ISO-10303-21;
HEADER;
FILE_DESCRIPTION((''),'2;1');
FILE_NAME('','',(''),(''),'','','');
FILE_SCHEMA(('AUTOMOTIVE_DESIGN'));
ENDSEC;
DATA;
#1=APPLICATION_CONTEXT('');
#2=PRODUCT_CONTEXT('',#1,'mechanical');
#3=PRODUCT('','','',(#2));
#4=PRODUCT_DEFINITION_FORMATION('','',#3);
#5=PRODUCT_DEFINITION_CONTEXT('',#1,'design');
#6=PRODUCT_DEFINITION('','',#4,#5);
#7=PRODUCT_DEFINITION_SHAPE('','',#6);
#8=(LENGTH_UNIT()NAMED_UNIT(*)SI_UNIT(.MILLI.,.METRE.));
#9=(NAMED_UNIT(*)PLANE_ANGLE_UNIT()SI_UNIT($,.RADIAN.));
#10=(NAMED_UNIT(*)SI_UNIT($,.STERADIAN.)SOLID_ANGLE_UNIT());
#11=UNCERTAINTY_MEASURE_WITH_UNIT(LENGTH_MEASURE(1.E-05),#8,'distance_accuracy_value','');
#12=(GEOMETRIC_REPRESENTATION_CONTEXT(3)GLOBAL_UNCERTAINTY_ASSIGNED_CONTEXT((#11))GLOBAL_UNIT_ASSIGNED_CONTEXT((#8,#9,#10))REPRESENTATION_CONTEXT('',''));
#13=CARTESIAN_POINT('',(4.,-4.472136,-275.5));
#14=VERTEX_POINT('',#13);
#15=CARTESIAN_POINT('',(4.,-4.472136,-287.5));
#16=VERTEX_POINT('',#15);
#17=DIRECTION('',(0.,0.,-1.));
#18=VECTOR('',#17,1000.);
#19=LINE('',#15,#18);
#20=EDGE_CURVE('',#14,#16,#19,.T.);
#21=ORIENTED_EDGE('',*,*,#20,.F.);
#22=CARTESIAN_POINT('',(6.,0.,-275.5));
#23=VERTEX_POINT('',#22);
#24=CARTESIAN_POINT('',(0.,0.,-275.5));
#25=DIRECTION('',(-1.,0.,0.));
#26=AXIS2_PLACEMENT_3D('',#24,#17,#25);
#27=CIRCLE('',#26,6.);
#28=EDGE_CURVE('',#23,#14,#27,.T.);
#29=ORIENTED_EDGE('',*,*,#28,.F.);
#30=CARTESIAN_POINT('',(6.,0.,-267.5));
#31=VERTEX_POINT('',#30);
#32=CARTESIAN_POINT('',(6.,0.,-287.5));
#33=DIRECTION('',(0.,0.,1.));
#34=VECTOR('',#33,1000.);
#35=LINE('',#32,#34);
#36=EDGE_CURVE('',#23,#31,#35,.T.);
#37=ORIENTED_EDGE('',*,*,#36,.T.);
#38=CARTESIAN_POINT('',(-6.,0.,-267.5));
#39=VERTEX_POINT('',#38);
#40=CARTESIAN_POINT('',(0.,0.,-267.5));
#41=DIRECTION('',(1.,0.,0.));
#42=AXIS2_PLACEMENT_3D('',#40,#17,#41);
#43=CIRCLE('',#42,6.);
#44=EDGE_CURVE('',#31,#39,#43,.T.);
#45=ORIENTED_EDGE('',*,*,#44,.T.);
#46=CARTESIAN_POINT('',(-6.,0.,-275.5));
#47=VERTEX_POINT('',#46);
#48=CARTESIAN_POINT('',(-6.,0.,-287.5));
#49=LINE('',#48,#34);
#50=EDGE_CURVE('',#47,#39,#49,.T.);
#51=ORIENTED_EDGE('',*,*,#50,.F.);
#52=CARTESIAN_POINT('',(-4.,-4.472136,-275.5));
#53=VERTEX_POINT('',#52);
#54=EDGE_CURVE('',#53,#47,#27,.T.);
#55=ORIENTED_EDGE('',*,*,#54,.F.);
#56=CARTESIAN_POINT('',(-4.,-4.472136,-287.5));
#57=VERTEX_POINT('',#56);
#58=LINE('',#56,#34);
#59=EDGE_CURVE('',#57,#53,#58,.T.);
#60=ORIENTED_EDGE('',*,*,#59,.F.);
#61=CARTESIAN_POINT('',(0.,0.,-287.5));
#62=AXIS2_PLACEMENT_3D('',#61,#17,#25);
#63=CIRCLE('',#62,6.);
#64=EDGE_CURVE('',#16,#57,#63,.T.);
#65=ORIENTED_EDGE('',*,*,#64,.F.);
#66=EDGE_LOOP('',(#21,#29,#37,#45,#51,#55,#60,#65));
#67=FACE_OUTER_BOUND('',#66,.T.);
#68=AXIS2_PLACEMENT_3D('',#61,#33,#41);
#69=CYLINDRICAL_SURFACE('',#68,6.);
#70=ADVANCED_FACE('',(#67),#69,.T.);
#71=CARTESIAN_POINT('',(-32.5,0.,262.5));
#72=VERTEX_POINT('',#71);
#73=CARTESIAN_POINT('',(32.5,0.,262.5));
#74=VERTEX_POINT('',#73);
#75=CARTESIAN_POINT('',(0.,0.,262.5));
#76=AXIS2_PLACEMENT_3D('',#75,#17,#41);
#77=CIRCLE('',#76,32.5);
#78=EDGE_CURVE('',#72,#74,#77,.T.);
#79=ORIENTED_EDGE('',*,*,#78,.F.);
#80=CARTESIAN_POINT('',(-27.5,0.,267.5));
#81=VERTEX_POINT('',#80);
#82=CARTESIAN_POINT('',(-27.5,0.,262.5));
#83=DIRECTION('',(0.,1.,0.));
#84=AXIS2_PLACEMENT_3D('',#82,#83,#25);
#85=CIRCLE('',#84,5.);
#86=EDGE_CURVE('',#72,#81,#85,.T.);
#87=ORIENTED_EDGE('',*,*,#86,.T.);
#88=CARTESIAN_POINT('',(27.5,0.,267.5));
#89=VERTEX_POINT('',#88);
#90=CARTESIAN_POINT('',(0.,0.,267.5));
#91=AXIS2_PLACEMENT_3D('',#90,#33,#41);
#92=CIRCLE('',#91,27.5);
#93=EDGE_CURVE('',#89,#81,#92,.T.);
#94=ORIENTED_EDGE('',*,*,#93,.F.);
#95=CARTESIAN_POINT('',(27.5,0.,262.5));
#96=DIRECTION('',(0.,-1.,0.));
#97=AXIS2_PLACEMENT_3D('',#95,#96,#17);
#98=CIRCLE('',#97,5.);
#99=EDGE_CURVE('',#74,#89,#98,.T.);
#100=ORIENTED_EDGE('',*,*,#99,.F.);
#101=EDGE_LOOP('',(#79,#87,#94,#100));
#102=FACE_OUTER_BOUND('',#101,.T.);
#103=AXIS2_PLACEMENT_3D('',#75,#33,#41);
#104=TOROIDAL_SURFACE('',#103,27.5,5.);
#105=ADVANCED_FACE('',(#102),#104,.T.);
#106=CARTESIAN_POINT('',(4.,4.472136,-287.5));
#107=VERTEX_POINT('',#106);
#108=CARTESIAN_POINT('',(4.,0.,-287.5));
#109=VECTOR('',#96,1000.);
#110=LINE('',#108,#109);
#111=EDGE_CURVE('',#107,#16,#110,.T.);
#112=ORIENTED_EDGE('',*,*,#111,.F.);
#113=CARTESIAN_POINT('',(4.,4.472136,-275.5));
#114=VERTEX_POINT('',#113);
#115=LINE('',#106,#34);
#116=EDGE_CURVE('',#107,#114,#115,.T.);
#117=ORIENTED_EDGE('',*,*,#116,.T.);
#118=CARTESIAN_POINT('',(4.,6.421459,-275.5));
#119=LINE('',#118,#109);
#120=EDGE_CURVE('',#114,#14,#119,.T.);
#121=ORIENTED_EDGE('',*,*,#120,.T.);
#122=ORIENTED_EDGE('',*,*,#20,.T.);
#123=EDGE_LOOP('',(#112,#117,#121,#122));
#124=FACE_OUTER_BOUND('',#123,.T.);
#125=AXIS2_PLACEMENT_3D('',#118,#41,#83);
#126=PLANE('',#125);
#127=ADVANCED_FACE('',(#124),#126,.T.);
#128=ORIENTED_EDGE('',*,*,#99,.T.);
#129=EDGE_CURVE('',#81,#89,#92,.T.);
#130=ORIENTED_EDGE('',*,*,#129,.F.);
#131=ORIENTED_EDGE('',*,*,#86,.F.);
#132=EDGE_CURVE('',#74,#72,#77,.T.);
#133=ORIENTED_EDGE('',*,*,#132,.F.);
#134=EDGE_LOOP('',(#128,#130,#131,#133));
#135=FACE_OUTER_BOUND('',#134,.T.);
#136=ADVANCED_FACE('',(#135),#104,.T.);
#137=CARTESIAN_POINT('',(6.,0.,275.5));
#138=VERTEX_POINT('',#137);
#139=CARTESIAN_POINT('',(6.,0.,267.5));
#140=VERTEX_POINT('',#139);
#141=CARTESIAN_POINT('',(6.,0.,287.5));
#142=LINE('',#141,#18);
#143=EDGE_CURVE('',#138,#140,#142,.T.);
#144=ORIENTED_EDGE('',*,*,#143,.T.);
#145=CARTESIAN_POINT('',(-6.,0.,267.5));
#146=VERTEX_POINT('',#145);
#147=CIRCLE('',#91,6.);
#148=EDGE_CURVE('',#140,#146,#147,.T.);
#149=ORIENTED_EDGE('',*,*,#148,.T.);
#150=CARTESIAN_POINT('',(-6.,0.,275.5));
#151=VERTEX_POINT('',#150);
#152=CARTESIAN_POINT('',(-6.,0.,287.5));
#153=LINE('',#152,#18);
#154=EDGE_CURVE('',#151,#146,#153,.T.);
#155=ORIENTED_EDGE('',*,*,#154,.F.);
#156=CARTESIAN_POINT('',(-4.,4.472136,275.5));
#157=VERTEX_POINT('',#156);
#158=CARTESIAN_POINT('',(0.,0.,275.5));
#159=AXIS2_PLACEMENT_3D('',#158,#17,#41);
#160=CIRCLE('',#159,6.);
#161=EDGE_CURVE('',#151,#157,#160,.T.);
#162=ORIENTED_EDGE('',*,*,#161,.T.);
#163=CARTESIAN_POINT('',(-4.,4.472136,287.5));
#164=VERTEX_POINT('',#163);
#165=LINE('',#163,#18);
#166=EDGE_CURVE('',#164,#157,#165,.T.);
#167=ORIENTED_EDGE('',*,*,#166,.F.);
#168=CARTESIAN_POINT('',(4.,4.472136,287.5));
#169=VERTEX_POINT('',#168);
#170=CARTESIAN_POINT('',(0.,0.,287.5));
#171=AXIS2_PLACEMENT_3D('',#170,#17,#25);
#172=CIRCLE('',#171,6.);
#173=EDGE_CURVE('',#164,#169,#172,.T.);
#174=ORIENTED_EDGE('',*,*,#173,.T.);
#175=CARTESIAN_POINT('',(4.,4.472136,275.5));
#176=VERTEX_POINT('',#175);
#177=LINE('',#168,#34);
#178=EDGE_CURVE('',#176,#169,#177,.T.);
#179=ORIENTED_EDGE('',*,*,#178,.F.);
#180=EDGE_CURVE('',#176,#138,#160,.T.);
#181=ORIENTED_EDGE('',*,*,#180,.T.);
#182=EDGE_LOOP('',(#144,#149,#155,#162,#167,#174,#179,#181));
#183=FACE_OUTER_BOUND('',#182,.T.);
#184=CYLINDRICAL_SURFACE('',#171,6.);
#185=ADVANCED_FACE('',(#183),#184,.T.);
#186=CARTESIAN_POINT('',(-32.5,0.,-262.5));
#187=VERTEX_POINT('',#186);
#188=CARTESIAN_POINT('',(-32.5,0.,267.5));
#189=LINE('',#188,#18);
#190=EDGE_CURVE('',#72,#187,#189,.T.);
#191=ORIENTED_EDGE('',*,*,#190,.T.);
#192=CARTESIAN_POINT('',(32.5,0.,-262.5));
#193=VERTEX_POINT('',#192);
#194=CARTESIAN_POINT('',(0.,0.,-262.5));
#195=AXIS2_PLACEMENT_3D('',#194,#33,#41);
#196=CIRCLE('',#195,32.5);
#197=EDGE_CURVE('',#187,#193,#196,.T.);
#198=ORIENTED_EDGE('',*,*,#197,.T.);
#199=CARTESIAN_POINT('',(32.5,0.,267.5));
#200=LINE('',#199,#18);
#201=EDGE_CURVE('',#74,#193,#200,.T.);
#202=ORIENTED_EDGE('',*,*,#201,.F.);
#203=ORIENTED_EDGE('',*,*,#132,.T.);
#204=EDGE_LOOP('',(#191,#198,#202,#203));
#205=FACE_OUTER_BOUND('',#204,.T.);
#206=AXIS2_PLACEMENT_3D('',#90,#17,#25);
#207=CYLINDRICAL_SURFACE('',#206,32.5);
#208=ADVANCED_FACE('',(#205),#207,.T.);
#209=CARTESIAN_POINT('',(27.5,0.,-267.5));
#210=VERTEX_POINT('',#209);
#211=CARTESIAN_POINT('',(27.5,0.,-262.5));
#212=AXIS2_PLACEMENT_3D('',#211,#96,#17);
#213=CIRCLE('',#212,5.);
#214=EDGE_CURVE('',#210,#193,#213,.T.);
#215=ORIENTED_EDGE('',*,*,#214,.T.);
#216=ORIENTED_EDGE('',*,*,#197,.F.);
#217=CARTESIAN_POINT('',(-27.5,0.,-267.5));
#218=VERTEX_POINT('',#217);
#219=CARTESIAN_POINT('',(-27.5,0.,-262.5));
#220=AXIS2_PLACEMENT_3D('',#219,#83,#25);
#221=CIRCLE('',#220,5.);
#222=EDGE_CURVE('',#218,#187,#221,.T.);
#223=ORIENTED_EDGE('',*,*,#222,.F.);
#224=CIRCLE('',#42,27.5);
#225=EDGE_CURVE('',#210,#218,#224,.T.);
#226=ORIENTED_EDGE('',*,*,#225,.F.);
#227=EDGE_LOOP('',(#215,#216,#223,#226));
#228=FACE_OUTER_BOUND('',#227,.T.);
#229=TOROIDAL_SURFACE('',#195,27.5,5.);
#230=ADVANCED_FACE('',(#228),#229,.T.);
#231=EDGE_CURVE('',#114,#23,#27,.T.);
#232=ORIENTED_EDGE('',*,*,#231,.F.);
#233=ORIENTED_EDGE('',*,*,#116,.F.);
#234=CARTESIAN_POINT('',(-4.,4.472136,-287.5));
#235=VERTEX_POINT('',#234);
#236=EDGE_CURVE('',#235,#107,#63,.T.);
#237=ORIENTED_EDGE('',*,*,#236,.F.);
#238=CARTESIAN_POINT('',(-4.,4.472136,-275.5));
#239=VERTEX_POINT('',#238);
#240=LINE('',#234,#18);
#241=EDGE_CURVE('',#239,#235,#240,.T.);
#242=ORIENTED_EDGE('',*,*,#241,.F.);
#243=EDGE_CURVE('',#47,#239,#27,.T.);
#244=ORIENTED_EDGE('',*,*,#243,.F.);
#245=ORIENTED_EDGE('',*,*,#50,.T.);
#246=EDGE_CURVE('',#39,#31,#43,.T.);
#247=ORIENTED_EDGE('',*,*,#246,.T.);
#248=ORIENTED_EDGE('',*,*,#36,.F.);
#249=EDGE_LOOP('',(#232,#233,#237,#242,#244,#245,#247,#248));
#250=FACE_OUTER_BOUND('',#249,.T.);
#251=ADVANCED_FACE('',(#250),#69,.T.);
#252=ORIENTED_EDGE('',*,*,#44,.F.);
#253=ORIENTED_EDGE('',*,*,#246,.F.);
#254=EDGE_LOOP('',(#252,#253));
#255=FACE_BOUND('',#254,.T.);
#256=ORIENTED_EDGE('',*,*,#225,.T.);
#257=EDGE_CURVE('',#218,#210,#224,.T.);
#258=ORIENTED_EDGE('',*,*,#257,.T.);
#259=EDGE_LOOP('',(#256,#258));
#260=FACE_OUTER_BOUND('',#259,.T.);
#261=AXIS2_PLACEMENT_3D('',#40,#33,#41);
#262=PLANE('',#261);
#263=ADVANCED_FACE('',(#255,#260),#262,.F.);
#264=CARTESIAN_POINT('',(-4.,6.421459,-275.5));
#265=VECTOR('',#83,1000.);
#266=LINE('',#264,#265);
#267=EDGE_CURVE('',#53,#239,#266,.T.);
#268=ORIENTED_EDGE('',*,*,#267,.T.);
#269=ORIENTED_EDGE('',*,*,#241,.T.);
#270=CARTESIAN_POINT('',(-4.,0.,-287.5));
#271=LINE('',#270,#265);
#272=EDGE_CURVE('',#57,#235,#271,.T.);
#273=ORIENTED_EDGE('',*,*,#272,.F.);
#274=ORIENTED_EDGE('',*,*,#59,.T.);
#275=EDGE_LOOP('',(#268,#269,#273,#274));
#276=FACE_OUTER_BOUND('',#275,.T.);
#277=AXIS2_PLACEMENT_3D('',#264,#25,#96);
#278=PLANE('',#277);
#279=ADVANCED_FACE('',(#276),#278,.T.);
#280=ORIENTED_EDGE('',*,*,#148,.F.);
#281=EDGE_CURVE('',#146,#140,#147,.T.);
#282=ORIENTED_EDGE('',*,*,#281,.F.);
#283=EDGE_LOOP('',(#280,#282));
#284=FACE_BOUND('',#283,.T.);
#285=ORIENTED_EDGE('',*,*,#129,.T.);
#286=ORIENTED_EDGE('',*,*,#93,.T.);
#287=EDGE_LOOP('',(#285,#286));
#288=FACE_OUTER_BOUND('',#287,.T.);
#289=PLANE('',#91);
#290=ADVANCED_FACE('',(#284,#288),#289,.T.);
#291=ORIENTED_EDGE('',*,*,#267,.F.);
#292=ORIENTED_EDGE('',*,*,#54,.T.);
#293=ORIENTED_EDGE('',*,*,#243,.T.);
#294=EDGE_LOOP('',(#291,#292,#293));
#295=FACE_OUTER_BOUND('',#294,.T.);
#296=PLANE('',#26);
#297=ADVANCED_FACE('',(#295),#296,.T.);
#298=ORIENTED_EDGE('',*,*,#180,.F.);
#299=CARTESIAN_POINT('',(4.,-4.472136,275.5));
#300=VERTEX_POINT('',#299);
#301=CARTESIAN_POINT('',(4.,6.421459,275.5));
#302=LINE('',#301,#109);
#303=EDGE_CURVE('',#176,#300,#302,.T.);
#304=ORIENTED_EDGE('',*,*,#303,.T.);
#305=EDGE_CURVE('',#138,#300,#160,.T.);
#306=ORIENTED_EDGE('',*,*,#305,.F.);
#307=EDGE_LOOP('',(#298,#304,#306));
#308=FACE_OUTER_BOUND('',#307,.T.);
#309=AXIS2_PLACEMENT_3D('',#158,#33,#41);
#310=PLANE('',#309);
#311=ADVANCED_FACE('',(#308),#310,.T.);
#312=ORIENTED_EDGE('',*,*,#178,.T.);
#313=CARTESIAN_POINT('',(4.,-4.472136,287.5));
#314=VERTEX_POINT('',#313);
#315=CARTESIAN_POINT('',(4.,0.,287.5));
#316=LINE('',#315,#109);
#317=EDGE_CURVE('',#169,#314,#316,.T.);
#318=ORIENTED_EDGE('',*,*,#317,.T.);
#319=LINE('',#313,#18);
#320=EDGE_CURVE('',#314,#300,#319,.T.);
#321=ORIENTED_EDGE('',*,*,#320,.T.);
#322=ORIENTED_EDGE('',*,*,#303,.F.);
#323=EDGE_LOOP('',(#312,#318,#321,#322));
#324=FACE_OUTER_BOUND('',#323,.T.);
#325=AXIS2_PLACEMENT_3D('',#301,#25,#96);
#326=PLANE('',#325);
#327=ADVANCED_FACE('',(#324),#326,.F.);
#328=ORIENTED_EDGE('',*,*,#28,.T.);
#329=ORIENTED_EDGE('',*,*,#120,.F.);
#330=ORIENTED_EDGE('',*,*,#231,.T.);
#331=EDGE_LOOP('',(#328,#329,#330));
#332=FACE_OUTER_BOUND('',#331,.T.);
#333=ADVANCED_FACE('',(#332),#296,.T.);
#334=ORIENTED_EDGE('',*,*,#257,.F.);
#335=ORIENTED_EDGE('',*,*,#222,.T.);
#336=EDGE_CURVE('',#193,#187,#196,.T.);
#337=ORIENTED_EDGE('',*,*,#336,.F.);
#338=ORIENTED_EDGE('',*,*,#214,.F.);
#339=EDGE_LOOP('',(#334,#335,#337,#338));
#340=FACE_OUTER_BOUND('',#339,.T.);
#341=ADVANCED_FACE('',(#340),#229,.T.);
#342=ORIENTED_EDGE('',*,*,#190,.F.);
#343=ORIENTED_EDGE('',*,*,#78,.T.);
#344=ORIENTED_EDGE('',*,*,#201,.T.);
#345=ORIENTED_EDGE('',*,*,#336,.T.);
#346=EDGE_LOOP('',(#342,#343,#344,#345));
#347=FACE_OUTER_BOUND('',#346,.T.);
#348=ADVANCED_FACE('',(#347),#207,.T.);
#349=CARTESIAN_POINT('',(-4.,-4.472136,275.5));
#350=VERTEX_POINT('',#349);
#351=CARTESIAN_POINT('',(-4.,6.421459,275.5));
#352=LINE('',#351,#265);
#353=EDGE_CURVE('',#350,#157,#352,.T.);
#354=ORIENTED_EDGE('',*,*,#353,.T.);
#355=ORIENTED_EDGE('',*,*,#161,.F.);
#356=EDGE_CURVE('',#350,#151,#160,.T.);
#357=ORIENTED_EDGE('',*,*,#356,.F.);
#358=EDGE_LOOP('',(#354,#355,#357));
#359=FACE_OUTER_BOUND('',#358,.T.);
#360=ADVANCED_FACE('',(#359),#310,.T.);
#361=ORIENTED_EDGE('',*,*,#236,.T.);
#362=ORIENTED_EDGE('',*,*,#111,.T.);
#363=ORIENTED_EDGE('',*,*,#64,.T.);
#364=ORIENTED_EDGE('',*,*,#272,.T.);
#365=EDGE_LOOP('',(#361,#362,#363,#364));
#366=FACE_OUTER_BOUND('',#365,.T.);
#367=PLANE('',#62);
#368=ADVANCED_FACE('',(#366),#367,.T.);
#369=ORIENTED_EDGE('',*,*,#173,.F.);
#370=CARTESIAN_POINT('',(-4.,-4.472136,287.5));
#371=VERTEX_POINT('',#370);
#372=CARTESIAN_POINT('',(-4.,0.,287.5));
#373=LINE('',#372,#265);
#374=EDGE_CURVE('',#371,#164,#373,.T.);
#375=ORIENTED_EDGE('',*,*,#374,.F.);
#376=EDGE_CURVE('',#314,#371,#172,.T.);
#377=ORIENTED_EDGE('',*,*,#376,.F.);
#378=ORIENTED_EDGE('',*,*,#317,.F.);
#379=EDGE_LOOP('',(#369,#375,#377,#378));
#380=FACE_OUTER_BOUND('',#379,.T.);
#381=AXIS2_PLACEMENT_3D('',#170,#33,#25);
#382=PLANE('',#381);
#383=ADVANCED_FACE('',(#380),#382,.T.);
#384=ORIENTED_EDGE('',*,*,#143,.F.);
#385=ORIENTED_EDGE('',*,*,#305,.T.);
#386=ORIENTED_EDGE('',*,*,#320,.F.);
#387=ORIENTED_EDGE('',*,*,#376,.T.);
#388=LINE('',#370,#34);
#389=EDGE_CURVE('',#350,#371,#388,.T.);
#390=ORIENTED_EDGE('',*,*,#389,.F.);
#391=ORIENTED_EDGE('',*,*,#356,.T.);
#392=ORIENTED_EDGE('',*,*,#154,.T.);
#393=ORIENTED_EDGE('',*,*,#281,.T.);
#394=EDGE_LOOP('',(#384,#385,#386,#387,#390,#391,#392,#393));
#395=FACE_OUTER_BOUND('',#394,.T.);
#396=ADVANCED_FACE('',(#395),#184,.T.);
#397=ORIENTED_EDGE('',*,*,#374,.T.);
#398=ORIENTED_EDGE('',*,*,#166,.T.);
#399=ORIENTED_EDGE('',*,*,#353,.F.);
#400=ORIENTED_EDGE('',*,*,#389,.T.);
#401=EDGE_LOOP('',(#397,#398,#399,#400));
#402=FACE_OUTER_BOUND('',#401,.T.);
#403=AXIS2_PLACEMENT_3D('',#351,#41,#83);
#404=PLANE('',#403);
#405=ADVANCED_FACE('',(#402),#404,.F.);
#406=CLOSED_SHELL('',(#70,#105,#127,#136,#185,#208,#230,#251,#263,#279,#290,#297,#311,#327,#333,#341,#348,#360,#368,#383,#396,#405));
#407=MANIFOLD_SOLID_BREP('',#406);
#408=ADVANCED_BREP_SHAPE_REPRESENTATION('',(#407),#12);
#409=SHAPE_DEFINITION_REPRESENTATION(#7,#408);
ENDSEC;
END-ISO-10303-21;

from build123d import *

# Parameters (mm, degrees)
SKETCH_1_R           = 32.5
EXTRUDE_1_DEPTH      = 267.5
SKETCH_2_R           = 6
EXTRUDE_2_DEPTH      = 20
SKETCH_3_OUTSIDE_W   = 179.512
SKETCH_3_OUTSIDE_H   = 179.512
SKETCH_3_OUTSIDE_W_2 = 8
SKETCH_3_OUTSIDE_H_2 = 12.842917612
CUT_EXTRUDE_1_DEPTH  = 12
FILLET_1_R           = 5


with BuildPart() as part:
    # 草图1 → 凸台-拉伸1 (new, symmetric)
    with BuildSketch(Plane.XY):
        Circle(SKETCH_1_R)
    extrude(amount=EXTRUDE_1_DEPTH, both=True)

    # 草图2 → 凸台-拉伸2 (add)
    with BuildSketch(Plane(origin=(0, 0, -267.5), x_dir=(-1, 0, 0), z_dir=(0, 0, -1))):
        with Locations(Location((0, 0, 0), (0, 0, 180))):
            Circle(SKETCH_2_R)
    extrude_2 = extrude(amount=EXTRUDE_2_DEPTH)

    # 草图3 outside → 切除-拉伸1 (cut)
    with BuildSketch(Plane(origin=(0, 0, -287.5), x_dir=(-1, 0, 0), z_dir=(0, 0, -1))):
        Rectangle(SKETCH_3_OUTSIDE_W, SKETCH_3_OUTSIDE_H)
        Rectangle(SKETCH_3_OUTSIDE_W_2, SKETCH_3_OUTSIDE_H_2, mode=Mode.SUBTRACT)
    cut_extrude_1 = extrude(amount=-CUT_EXTRUDE_1_DEPTH, mode=Mode.SUBTRACT)

    # 镜向1: 凸台-拉伸2, 切除-拉伸1 across plane
    add(extrude_2.mirror(Plane.XY))
    add(cut_extrude_1.mirror(Plane.XY), mode=Mode.SUBTRACT)

    # 圆角1
    fillet_1_edges = [part.edges().sort_by_distance(p)[0] for p in [
        (-32.5, 0, -267.5),
        (-32.5, 0, 267.5),
    ]]
    fillet(fillet_1_edges, radius=FILLET_1_R)


solid = part.part
